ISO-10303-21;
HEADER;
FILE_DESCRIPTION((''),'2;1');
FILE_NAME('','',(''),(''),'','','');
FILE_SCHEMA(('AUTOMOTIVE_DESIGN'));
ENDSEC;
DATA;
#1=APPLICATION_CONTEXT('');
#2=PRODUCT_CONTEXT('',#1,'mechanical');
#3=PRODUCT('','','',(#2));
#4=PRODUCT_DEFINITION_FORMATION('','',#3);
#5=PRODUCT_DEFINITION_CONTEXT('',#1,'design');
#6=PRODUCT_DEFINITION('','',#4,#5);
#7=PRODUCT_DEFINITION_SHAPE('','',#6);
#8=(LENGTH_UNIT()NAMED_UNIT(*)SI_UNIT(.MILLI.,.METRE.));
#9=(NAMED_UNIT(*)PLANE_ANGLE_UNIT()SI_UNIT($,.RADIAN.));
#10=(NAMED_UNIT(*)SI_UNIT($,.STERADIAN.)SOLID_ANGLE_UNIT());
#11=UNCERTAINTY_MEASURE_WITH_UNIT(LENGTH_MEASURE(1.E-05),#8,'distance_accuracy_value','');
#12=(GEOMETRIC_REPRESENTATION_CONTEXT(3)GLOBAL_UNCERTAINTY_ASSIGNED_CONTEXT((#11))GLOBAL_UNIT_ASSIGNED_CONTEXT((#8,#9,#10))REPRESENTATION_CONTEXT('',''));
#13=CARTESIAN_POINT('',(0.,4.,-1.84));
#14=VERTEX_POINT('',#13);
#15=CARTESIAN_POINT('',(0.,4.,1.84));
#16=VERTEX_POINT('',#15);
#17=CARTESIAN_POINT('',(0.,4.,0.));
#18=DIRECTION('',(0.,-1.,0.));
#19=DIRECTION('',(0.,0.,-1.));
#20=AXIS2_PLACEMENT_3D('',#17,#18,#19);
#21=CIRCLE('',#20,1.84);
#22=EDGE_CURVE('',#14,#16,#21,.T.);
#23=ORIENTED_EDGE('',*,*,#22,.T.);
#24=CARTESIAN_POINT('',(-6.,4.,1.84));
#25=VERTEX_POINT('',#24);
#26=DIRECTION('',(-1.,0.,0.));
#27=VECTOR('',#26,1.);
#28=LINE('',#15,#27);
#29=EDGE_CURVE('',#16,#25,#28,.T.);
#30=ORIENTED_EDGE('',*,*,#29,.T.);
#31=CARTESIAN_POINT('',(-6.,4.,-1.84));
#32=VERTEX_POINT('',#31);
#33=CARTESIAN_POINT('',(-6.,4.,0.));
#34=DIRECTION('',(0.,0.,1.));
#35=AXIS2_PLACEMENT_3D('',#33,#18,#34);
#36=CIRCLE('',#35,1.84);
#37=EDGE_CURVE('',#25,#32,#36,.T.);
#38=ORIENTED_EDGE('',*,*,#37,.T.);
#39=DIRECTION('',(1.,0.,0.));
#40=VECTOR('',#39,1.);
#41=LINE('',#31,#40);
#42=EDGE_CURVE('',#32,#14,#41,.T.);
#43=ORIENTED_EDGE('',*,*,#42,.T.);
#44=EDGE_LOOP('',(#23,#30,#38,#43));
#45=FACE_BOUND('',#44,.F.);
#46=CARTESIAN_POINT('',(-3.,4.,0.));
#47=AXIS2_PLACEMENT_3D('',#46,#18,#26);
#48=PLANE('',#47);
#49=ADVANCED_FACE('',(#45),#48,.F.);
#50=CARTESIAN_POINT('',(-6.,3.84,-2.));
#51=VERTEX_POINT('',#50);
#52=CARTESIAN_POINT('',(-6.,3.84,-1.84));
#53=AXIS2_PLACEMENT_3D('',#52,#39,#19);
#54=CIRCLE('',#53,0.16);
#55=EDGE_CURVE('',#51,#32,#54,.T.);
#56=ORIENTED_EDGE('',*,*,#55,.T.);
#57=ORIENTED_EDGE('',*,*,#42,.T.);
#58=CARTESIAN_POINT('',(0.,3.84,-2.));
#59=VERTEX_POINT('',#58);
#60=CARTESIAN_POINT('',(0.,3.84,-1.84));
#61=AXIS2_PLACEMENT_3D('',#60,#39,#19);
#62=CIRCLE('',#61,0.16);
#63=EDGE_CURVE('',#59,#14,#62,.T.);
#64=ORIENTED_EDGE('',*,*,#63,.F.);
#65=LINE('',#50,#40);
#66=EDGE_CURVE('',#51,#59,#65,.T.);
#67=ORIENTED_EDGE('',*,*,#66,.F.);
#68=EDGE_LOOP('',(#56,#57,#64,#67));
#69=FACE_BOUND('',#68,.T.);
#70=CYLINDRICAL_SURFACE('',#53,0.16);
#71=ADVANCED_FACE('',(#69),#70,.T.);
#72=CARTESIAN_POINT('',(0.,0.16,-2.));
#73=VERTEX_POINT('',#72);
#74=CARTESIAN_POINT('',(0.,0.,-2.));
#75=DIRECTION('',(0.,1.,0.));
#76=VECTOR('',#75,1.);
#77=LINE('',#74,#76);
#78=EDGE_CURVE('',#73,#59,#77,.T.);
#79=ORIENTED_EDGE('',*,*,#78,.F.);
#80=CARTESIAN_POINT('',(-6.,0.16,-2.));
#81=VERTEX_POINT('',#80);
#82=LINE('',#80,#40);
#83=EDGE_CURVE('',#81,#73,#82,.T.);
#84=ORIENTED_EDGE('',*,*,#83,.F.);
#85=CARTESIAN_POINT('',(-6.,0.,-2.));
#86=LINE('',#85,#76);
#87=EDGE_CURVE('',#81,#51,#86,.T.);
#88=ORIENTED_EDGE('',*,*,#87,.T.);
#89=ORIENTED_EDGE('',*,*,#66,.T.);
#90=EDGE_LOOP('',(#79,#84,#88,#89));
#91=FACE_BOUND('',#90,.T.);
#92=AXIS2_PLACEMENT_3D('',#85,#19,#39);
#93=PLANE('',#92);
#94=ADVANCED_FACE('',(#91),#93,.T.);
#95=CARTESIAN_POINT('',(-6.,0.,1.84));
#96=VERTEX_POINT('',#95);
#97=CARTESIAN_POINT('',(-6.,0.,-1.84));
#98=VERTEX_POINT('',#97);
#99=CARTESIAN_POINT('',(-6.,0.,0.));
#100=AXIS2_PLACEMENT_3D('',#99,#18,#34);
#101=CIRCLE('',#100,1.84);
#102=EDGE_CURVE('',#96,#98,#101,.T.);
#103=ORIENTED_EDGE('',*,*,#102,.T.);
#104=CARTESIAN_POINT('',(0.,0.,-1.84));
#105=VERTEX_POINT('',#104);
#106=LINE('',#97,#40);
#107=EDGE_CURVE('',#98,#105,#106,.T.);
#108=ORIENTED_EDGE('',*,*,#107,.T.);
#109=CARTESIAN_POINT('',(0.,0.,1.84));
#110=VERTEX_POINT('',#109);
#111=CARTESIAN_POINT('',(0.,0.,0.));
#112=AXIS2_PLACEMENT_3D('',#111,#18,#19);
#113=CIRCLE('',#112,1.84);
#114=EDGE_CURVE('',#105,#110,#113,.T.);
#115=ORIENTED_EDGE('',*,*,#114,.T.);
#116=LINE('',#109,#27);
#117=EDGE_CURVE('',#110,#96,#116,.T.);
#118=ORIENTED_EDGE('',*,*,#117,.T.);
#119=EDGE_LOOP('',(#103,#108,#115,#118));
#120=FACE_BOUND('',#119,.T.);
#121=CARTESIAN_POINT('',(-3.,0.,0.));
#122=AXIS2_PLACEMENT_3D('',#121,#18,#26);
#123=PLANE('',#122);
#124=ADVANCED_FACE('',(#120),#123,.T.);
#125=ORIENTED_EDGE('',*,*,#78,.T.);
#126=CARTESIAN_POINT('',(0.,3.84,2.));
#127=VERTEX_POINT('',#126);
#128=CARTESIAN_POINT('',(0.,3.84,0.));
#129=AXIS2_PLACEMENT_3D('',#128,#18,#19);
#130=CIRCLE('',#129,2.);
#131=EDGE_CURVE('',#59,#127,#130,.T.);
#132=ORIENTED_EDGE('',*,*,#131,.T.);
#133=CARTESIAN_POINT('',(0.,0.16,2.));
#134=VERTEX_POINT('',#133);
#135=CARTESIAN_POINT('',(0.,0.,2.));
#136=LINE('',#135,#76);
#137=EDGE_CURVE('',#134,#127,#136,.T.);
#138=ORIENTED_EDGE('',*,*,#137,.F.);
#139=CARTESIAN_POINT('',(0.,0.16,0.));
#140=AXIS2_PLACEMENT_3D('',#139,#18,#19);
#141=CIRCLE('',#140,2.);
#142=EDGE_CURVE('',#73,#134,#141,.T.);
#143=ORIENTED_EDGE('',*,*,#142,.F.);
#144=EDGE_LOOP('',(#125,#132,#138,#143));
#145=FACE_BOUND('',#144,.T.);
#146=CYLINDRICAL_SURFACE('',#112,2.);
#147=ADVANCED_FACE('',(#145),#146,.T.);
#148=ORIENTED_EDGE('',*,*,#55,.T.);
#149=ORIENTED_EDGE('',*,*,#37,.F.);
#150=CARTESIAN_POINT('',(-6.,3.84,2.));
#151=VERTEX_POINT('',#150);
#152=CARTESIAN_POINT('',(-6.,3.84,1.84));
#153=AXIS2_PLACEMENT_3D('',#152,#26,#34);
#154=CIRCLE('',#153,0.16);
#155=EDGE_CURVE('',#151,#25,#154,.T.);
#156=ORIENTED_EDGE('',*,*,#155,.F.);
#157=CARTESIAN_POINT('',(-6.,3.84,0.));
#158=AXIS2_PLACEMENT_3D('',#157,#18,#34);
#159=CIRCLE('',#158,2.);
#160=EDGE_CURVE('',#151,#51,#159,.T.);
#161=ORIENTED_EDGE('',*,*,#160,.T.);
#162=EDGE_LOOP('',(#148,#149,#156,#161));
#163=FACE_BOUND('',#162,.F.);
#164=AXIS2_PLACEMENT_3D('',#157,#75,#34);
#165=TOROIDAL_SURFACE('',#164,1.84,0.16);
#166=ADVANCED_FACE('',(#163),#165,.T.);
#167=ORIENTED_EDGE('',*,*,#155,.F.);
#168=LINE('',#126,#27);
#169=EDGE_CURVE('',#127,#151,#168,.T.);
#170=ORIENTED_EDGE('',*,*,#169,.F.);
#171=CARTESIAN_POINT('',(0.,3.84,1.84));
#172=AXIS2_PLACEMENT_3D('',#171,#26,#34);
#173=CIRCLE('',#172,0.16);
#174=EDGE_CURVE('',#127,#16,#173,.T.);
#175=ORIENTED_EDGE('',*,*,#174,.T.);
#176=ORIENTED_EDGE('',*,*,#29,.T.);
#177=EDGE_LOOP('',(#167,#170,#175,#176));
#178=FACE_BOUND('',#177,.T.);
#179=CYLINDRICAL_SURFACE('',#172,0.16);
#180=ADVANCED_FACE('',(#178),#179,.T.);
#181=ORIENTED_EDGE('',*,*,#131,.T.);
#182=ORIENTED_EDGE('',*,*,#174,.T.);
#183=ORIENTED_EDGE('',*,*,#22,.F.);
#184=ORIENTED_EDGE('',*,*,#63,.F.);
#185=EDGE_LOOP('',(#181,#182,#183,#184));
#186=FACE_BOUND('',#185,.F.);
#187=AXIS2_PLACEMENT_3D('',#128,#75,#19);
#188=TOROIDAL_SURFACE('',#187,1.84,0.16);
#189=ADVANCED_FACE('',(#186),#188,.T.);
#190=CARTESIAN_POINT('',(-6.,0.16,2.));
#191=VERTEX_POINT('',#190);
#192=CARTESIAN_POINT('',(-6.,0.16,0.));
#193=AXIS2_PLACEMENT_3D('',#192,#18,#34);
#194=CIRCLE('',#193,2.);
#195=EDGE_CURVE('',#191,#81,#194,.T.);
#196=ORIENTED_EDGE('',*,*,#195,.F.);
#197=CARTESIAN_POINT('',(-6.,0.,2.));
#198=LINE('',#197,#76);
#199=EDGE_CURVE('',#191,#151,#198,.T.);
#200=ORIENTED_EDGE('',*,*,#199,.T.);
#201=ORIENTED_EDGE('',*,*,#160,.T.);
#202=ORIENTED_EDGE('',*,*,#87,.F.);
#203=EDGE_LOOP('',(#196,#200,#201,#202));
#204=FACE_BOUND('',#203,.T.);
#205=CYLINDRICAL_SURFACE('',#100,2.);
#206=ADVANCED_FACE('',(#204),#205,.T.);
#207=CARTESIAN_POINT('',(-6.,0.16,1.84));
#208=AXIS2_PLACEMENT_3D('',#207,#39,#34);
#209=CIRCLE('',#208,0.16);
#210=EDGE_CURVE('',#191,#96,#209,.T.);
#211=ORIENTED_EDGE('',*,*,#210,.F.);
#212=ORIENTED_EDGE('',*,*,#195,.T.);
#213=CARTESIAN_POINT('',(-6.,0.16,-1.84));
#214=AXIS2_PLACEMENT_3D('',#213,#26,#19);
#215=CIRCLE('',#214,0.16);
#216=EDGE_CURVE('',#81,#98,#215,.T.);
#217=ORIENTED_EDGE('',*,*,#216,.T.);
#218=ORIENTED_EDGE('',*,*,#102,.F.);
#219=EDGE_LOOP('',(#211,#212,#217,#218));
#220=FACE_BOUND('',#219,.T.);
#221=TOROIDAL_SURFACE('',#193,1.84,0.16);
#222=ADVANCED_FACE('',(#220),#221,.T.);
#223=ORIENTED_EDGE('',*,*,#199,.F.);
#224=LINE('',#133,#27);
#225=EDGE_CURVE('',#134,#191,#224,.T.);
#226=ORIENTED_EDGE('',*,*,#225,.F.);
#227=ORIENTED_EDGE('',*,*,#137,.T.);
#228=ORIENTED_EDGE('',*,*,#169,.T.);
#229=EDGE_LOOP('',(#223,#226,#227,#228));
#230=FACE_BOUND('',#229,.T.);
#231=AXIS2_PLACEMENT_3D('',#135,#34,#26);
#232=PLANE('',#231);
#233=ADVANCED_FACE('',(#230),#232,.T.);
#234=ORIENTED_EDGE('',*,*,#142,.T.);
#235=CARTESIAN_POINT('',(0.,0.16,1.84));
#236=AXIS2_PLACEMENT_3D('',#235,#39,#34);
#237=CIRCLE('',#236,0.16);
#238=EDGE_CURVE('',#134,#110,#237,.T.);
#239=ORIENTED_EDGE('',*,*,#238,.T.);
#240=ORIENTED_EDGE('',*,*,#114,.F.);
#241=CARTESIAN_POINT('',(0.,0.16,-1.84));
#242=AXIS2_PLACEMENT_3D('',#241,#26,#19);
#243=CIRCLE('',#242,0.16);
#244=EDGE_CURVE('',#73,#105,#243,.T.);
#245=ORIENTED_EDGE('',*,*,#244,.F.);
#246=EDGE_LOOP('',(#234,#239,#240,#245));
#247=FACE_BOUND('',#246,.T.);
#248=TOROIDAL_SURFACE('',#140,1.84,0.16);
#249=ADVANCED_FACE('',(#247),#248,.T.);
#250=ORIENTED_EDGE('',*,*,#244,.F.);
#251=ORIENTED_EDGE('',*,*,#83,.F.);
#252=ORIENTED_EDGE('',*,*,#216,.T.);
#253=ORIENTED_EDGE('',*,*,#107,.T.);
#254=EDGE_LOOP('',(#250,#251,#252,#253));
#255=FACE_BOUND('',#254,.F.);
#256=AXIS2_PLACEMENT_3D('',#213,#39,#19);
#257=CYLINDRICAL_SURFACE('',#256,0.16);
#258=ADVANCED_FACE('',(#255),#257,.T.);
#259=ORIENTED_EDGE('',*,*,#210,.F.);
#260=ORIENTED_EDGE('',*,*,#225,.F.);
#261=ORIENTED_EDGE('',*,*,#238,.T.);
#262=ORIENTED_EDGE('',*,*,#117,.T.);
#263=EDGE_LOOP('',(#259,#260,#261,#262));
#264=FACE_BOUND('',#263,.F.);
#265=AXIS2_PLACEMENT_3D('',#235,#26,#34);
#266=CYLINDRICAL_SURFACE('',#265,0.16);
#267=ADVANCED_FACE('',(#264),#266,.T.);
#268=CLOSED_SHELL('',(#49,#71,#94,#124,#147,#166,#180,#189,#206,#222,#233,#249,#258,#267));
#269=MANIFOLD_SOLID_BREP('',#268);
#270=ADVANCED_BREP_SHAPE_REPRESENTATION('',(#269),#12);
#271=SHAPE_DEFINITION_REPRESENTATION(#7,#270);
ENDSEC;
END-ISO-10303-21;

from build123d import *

# Parameters (mm, degrees)
EXTRUDE1_DEPTH = 4
FILLET1_R      = 0.16


with BuildPart() as part:
    # Sketch1 → Extrude1 (new body)
    with BuildSketch(Plane(origin=(0, 0, 0), x_dir=(1, 0, 0), z_dir=(0, 1, 0))):
        with BuildLine():
            Line((-6, 2), (0, 2))
            ThreePointArc((0, 2), (2, 0), (0, -2))
            Line((0, -2), (-6, -2))
            ThreePointArc((-6, -2), (-8, 0), (-6, 2))
        make_face()
    extrude(amount=EXTRUDE1_DEPTH)

    # Fillet1
    fillet1_edges = [part.edges().sort_by_distance(p)[0] for p in [
        (2, 4, 0),
        (-3, 4, -2),
        (-8, 4, 0),
        (-3, 0, -2),
        (2, 0, 0),
        (-3, 0, 2),
        (-8, 0, 0),
        (-3, 4, 2),
    ]]
    fillet(fillet1_edges, radius=FILLET1_R)


solid = part.part
